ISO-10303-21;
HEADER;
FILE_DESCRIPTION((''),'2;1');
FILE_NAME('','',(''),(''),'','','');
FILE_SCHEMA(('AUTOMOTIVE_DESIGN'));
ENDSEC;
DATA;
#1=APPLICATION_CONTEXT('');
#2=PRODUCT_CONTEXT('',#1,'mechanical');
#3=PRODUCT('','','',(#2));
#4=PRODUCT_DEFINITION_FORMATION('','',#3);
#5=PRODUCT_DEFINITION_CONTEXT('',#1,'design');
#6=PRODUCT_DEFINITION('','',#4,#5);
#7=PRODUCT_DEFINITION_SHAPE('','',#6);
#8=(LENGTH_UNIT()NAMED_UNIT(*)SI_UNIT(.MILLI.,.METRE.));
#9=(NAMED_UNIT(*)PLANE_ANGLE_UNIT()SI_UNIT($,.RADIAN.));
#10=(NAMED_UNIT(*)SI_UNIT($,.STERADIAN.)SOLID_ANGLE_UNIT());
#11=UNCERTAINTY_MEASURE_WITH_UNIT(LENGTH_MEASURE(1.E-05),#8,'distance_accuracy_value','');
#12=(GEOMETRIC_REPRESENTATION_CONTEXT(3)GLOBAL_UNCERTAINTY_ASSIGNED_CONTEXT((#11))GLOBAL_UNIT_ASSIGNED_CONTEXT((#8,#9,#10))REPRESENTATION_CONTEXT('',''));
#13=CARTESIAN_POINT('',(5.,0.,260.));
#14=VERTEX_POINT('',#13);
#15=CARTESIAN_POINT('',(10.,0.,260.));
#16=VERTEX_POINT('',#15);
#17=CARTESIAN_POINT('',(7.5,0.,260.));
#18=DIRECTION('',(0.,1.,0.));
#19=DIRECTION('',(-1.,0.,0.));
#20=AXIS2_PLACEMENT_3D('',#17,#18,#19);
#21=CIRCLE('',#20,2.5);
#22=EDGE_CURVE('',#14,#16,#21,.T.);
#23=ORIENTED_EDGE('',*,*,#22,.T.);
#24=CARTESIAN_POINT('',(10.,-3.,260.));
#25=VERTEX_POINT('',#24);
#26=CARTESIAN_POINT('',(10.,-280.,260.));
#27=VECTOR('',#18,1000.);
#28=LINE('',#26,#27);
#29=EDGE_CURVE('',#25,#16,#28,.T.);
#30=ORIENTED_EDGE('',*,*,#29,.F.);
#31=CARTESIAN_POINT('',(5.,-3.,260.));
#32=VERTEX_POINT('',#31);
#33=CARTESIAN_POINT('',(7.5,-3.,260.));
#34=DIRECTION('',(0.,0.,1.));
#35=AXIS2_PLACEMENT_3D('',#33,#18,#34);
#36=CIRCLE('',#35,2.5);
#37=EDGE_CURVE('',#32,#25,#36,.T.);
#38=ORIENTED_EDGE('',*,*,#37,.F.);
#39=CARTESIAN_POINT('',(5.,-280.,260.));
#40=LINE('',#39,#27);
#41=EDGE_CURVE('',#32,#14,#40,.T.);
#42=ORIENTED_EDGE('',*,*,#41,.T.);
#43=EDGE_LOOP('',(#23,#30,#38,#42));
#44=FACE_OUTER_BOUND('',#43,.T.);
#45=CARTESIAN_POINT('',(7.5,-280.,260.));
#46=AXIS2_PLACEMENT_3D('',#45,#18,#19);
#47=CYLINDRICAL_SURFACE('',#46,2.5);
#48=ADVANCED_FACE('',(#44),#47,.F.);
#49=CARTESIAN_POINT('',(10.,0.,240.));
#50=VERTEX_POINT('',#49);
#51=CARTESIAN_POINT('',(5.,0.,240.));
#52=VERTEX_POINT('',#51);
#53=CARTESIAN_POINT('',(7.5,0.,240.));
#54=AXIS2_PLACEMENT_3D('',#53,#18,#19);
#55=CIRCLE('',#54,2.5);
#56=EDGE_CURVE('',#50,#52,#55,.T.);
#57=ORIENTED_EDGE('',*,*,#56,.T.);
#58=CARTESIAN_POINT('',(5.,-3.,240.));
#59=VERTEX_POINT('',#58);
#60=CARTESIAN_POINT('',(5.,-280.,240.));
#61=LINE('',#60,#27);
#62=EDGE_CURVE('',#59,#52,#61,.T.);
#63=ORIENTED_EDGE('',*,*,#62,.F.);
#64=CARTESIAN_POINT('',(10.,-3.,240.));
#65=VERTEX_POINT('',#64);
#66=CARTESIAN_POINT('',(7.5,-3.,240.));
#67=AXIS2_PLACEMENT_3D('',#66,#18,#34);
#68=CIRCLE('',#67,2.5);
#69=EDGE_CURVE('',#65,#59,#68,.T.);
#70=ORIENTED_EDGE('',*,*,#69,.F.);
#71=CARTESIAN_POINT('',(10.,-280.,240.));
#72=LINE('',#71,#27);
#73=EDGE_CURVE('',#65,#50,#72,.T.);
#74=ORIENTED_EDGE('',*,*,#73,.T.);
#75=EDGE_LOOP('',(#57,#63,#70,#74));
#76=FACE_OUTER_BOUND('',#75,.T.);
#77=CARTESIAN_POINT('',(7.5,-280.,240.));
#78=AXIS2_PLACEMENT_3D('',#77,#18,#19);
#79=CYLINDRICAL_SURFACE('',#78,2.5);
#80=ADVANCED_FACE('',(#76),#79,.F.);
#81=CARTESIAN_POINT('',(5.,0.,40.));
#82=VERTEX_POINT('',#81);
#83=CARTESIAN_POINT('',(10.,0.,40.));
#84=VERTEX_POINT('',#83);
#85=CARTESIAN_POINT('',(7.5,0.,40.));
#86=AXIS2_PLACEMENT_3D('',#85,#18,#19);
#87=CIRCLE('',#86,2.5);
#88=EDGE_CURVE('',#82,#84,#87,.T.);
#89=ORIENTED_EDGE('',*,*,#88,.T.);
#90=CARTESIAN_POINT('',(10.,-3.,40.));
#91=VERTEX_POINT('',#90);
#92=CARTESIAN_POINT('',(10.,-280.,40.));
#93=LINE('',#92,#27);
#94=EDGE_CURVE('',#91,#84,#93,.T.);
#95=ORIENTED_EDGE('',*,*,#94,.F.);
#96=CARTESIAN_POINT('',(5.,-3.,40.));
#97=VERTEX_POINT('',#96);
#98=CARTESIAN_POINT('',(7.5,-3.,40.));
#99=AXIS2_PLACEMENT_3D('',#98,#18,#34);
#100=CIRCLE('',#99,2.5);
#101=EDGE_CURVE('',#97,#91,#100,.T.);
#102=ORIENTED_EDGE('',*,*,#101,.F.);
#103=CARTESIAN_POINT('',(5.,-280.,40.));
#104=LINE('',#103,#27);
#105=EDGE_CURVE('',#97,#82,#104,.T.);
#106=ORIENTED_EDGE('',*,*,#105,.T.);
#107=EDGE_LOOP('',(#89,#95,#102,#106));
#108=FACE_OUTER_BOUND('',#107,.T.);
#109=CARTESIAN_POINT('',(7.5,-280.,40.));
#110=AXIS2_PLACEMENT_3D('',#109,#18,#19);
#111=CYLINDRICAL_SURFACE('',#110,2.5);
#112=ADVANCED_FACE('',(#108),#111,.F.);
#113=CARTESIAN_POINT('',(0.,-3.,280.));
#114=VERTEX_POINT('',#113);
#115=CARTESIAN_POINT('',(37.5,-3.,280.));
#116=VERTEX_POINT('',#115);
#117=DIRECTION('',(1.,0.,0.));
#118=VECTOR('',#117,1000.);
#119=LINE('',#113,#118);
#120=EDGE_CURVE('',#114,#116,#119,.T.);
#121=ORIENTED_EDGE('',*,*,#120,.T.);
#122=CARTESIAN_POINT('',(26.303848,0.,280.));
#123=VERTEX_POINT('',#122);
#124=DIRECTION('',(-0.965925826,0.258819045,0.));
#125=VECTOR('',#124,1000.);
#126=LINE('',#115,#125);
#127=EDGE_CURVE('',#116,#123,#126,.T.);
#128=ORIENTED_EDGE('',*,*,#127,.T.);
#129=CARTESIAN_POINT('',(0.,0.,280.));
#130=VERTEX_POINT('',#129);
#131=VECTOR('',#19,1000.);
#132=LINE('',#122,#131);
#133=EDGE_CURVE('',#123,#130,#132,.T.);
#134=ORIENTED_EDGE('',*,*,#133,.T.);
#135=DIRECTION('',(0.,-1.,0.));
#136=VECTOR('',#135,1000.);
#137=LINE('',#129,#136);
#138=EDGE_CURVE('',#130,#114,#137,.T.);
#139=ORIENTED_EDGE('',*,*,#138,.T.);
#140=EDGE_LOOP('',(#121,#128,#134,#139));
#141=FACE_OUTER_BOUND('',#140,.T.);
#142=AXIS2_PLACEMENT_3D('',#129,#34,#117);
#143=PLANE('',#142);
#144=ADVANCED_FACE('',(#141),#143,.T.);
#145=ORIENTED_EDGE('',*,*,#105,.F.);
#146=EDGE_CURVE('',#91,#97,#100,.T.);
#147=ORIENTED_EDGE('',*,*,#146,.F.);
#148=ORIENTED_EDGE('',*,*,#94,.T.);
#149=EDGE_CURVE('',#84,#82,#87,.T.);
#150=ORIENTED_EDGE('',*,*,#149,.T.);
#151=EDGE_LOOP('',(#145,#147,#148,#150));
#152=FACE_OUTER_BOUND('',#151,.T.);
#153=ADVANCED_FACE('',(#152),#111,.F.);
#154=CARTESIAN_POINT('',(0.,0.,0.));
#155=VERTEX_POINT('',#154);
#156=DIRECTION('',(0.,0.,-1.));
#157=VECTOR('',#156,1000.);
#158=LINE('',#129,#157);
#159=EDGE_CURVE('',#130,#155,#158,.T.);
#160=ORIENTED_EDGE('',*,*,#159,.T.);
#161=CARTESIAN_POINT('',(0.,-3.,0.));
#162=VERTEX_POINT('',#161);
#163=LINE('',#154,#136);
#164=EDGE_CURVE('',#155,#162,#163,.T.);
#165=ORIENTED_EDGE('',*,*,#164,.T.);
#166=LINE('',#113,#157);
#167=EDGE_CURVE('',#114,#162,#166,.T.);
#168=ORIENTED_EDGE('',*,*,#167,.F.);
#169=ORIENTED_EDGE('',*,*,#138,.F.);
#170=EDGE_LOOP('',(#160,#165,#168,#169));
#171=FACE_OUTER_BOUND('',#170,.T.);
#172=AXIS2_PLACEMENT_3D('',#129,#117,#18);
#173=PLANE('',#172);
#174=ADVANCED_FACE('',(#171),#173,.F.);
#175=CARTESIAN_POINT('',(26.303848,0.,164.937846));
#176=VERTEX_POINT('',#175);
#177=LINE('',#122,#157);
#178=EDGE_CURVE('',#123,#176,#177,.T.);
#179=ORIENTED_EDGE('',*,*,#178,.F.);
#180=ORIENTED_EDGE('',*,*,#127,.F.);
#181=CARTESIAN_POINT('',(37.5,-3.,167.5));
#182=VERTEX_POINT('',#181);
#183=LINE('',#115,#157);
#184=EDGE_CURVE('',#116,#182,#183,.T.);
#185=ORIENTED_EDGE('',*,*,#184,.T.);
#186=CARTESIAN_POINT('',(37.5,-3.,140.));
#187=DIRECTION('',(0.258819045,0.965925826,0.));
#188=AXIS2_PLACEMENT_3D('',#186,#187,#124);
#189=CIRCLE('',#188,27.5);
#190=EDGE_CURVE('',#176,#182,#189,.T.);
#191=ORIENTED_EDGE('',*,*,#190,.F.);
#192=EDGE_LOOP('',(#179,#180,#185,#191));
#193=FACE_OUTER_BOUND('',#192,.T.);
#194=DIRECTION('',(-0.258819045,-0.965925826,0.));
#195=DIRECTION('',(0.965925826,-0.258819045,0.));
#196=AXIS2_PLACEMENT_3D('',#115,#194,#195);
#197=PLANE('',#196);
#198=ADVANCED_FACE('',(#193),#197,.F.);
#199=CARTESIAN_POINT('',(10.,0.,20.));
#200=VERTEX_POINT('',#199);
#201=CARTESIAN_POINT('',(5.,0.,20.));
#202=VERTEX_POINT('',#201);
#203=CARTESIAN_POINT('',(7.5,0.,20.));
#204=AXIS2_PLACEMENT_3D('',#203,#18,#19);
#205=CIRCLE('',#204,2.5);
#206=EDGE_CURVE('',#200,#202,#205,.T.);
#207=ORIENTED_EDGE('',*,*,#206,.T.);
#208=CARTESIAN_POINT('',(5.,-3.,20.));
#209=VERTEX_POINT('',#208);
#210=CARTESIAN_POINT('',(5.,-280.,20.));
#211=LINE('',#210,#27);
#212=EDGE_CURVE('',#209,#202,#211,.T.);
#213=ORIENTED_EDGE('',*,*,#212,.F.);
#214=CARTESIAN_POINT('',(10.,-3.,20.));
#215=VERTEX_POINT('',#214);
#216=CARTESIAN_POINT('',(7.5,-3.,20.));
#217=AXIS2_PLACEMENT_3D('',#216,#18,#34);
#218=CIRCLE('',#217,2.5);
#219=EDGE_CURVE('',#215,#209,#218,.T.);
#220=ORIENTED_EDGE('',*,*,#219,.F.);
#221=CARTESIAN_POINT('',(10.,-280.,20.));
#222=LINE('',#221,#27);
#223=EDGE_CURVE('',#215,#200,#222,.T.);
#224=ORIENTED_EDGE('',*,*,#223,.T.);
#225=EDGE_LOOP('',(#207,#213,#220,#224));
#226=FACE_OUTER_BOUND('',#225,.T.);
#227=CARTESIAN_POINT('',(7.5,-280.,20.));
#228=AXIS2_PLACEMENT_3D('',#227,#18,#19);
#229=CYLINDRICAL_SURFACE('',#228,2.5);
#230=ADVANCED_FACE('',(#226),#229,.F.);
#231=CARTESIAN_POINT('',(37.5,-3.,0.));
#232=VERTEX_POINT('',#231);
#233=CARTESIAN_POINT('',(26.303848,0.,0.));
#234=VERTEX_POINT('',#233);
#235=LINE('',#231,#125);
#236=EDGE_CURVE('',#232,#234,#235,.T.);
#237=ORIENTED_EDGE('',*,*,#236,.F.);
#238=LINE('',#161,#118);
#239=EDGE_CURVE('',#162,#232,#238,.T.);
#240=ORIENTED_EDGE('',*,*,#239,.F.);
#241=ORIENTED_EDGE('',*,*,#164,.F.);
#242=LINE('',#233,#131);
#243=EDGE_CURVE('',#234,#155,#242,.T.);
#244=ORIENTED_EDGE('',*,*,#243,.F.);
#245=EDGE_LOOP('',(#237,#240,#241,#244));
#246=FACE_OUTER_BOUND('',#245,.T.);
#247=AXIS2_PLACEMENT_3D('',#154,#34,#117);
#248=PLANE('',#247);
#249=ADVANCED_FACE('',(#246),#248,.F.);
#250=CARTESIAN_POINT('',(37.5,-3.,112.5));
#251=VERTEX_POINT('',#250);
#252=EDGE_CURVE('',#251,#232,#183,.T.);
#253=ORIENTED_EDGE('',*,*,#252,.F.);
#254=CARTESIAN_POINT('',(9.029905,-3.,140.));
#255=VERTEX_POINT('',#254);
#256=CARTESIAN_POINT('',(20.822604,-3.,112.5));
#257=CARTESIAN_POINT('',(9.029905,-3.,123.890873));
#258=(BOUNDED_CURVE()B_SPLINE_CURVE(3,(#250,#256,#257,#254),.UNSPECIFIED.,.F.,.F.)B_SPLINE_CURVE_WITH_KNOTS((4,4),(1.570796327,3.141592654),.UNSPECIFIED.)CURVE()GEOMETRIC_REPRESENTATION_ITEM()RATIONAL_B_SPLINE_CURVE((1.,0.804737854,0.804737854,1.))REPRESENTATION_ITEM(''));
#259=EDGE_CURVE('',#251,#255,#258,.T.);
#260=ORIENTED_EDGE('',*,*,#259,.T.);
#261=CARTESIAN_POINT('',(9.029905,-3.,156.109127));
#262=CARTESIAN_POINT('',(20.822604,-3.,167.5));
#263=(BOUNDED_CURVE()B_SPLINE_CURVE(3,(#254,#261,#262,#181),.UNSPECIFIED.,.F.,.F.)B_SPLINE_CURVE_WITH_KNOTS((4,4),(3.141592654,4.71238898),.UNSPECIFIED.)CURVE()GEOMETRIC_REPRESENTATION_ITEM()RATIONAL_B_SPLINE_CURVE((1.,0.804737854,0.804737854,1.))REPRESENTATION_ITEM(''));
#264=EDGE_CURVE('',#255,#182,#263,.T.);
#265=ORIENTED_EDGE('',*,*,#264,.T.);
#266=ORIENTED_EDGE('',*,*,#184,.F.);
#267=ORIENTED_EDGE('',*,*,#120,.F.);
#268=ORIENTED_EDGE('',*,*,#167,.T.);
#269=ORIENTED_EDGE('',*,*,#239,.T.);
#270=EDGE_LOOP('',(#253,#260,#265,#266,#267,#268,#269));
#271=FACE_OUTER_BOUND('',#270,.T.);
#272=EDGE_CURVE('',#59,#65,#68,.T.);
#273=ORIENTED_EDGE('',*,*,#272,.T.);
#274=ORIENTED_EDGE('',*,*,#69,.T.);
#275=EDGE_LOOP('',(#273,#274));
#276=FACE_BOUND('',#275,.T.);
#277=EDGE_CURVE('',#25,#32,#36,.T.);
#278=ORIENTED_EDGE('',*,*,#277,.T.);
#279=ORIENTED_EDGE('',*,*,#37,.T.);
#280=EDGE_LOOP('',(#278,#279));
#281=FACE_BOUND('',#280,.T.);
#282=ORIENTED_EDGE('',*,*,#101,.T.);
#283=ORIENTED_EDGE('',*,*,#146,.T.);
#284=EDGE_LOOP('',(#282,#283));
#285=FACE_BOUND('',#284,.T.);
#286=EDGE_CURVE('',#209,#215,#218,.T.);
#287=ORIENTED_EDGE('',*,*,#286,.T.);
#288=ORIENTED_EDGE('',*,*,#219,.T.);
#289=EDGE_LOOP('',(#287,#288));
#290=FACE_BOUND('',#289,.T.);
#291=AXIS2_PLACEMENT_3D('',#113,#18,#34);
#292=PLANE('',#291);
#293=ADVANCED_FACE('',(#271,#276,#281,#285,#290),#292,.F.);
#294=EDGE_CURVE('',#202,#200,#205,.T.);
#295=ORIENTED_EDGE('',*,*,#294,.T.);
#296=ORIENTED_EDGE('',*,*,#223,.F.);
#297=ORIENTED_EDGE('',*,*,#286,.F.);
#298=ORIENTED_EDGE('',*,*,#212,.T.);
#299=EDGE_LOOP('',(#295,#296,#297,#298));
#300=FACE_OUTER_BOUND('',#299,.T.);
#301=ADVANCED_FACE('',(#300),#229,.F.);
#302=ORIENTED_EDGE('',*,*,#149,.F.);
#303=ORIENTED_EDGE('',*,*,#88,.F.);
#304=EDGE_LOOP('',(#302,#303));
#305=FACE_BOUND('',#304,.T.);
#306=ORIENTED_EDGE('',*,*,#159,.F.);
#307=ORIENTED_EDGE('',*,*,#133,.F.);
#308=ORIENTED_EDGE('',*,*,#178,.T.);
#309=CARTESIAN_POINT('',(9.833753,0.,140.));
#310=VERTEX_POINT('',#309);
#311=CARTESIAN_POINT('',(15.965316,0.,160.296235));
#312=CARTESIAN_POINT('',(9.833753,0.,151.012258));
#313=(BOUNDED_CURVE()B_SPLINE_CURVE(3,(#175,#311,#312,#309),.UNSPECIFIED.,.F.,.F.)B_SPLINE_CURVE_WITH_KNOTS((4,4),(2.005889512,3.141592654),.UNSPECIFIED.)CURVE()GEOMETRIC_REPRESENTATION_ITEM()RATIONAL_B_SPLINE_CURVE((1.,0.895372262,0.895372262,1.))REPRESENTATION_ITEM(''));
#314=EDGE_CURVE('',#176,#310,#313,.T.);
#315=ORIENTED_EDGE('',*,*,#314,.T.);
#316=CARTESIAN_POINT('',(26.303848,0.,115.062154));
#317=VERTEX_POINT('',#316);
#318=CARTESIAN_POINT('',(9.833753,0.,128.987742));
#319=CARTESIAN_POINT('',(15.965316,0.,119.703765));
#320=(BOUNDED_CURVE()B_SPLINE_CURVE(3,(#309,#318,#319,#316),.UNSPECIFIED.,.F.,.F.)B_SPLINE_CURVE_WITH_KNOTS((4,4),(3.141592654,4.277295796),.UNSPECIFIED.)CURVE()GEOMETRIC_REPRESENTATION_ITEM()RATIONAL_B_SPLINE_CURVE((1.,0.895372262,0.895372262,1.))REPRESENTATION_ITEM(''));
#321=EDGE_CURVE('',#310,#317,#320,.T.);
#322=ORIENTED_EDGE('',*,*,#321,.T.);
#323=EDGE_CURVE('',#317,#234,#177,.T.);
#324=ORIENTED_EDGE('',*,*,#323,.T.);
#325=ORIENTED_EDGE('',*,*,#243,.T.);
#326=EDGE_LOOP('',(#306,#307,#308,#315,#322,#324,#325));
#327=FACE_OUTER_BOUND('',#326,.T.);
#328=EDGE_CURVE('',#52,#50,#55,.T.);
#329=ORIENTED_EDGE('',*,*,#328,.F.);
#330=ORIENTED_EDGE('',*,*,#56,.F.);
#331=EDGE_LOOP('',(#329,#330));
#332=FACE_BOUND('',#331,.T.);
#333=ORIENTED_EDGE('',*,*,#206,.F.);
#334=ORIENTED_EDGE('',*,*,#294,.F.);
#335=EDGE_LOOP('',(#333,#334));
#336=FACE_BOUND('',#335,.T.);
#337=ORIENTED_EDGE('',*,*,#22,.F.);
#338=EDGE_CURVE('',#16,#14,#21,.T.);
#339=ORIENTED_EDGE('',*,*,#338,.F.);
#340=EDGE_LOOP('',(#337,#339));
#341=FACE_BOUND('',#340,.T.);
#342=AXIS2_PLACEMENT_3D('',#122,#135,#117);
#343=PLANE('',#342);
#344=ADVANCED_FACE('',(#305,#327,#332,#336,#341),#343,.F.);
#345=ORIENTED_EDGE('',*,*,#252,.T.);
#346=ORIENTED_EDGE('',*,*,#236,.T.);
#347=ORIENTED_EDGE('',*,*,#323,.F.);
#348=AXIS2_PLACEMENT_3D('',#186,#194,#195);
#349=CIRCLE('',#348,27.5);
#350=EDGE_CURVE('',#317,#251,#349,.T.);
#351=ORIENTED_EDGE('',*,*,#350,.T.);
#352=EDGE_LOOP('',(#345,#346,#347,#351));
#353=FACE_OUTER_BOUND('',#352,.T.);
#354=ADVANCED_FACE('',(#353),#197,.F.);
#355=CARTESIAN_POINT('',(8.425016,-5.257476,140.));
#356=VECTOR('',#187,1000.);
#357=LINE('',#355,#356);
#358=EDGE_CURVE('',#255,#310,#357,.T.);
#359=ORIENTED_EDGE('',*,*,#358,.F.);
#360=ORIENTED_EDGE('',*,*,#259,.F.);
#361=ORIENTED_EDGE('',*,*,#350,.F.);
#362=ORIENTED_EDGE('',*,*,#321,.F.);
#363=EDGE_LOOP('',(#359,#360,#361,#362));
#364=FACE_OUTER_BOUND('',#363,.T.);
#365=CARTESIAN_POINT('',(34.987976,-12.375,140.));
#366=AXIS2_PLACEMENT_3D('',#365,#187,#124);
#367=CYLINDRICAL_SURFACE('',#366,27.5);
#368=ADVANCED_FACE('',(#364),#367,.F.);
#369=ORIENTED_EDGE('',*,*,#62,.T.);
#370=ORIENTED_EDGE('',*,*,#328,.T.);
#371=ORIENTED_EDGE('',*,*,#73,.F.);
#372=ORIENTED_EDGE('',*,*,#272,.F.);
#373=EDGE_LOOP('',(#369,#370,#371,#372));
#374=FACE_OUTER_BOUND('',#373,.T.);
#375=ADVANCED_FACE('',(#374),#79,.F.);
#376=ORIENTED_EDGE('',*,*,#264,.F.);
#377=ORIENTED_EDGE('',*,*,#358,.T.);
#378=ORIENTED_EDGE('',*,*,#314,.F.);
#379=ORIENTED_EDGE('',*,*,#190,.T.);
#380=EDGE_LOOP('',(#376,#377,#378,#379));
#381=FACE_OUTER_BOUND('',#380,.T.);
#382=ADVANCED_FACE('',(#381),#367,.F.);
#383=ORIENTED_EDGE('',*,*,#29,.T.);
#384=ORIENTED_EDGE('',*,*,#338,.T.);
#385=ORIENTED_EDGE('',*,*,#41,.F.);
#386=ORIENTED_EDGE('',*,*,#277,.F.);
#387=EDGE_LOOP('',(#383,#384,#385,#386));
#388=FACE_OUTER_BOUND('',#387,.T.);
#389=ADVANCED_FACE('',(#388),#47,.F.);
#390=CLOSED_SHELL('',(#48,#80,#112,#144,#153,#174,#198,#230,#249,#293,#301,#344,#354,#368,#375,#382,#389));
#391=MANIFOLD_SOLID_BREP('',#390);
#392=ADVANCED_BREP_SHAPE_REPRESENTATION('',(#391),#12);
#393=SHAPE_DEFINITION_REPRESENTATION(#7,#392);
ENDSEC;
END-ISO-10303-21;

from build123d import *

# Parameters (mm, degrees)
EXTRUDE_1_DEPTH     = 280
SKETCH_2_R          = 2.5
CUT_EXTRUDE_1_DEPTH = 280
SKETCH_3_R          = 27.5
CUT_EXTRUDE_5_DEPTH = 283.433889606


with BuildPart() as part:
    # 草图1 → 凸台-拉伸1 (new body)
    with BuildSketch(Plane.XY):
        Polygon((0, 0), (0, -3), (37.5, -3), (26.303847577, 0), align=None)
    extrude(amount=EXTRUDE_1_DEPTH)

    # 草图2 → 切除-拉伸1 (cut)
    with BuildSketch(Plane(origin=(0, 0, 0), x_dir=(1, 0, 0), z_dir=(0, 1, 0))):
        with Locations(Location((7.5, -260, 0), (0, 0, 180))):
            Circle(SKETCH_2_R)
        with Locations(Location((7.5, -240, 0), (0, 0, 180))):
            Circle(SKETCH_2_R)
        with Locations(Location((7.5, -20, 0), (0, 0, 180))):
            Circle(SKETCH_2_R)
        with Locations(Location((7.5, -40, 0), (0, 0, 180))):
            Circle(SKETCH_2_R)
    extrude(amount=-CUT_EXTRUDE_1_DEPTH, mode=Mode.SUBTRACT)

    # 草图3 → 切除-拉伸5 (cut, through all)
    with BuildSketch(Plane(origin=(1.762023679, 6.575961894, 0), x_dir=(0.96592582628907, -0.2588190451025147, 0), z_dir=(0.25881904510251463, 0.9659258262890699, 0))):
        with Locations((36.998675621, -140)):
            Circle(SKETCH_3_R)
    extrude(amount=-CUT_EXTRUDE_5_DEPTH, mode=Mode.SUBTRACT)


solid = part.part
